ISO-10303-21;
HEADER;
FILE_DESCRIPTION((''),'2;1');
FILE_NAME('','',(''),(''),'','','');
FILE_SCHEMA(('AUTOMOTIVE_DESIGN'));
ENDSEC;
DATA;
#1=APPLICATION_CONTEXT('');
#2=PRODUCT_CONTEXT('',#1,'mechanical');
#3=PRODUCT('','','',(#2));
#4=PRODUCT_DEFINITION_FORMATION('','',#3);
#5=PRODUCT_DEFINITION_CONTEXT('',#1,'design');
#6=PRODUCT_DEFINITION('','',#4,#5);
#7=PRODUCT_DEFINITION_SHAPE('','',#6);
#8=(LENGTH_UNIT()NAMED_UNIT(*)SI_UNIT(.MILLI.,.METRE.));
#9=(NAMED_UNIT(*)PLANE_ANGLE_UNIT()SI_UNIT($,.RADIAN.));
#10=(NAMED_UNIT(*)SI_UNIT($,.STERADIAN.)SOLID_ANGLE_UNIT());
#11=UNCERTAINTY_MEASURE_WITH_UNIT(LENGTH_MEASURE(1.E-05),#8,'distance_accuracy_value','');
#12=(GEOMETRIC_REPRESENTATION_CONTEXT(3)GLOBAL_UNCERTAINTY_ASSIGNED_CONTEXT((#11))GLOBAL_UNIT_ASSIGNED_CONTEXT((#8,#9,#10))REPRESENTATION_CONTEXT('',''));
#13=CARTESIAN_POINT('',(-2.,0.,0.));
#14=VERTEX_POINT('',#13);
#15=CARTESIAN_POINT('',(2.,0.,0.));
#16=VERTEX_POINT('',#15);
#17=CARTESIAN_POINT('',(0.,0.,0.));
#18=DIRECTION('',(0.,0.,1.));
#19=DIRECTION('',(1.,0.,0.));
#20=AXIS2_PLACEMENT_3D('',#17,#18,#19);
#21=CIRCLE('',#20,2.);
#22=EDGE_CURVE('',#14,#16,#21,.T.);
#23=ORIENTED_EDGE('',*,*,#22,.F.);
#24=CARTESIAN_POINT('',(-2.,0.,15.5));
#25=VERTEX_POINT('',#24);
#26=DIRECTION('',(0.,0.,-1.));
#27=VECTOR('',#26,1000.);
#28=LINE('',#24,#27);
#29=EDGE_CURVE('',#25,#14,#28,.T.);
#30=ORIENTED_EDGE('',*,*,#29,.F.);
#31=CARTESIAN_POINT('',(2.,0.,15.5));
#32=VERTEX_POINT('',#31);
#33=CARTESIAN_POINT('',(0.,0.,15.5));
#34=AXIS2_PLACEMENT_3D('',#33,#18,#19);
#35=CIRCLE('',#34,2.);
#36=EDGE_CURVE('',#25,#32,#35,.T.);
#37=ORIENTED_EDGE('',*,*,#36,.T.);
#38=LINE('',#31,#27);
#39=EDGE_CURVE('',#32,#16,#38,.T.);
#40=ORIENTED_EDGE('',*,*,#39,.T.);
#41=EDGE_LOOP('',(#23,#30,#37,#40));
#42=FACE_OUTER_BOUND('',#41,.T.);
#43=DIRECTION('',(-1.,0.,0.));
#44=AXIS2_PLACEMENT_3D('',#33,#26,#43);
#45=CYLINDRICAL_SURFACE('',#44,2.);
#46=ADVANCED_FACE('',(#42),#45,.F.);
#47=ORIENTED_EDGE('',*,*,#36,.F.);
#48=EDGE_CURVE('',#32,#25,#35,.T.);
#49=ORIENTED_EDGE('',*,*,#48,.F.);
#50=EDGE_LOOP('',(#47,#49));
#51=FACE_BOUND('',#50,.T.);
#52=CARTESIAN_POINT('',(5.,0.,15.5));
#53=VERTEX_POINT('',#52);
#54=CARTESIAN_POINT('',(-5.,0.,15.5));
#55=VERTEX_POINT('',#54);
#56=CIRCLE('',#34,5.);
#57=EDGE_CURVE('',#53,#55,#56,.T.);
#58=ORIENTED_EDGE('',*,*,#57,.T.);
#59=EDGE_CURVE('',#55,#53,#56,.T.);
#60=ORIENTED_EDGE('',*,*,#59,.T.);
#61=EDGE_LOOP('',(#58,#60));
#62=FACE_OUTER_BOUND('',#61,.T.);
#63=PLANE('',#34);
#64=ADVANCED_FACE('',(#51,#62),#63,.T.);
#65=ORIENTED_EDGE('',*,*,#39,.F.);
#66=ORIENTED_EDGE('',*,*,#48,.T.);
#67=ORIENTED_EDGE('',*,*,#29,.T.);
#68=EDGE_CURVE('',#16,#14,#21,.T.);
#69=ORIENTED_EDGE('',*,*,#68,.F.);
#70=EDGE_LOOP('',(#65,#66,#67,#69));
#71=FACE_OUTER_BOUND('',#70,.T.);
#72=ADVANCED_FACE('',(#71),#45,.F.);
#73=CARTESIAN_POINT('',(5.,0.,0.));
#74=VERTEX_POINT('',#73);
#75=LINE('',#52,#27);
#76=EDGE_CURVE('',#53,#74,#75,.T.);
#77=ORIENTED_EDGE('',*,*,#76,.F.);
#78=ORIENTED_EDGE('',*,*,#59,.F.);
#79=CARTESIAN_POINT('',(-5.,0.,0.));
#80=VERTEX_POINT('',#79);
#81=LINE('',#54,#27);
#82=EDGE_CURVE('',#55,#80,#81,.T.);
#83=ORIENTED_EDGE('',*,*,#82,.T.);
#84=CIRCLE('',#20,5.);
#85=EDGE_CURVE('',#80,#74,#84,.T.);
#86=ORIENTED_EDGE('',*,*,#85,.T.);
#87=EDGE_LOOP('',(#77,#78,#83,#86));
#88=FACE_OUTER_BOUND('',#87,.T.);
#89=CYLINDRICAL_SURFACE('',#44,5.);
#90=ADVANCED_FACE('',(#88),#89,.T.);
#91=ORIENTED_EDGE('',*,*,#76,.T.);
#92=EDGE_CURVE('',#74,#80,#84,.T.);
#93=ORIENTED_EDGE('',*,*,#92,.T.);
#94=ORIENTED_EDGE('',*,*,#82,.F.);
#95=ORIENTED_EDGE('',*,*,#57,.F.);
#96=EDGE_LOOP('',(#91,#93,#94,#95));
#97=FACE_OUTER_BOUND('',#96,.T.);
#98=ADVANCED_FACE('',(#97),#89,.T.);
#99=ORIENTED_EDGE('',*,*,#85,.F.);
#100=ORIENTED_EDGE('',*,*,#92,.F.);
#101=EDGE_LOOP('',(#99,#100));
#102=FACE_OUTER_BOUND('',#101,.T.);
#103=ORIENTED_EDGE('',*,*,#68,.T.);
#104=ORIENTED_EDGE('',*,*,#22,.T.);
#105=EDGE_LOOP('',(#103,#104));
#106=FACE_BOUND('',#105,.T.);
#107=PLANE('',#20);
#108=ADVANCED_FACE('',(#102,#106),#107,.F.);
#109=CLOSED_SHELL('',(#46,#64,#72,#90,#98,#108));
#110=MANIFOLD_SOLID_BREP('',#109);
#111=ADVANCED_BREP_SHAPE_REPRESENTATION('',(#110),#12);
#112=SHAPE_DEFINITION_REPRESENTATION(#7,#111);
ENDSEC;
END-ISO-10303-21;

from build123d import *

# Parameters (mm, degrees)
SKETCH_1_R      = 5
SKETCH_1_R_2    = 2
EXTRUDE_1_DEPTH = 15.5


with BuildPart() as part:
    # 草图1 → 凸台-拉伸1 (new body)
    with BuildSketch(Plane.XY):
        Circle(SKETCH_1_R)
        Circle(SKETCH_1_R_2, mode=Mode.SUBTRACT)
    extrude(amount=EXTRUDE_1_DEPTH)


solid = part.part
